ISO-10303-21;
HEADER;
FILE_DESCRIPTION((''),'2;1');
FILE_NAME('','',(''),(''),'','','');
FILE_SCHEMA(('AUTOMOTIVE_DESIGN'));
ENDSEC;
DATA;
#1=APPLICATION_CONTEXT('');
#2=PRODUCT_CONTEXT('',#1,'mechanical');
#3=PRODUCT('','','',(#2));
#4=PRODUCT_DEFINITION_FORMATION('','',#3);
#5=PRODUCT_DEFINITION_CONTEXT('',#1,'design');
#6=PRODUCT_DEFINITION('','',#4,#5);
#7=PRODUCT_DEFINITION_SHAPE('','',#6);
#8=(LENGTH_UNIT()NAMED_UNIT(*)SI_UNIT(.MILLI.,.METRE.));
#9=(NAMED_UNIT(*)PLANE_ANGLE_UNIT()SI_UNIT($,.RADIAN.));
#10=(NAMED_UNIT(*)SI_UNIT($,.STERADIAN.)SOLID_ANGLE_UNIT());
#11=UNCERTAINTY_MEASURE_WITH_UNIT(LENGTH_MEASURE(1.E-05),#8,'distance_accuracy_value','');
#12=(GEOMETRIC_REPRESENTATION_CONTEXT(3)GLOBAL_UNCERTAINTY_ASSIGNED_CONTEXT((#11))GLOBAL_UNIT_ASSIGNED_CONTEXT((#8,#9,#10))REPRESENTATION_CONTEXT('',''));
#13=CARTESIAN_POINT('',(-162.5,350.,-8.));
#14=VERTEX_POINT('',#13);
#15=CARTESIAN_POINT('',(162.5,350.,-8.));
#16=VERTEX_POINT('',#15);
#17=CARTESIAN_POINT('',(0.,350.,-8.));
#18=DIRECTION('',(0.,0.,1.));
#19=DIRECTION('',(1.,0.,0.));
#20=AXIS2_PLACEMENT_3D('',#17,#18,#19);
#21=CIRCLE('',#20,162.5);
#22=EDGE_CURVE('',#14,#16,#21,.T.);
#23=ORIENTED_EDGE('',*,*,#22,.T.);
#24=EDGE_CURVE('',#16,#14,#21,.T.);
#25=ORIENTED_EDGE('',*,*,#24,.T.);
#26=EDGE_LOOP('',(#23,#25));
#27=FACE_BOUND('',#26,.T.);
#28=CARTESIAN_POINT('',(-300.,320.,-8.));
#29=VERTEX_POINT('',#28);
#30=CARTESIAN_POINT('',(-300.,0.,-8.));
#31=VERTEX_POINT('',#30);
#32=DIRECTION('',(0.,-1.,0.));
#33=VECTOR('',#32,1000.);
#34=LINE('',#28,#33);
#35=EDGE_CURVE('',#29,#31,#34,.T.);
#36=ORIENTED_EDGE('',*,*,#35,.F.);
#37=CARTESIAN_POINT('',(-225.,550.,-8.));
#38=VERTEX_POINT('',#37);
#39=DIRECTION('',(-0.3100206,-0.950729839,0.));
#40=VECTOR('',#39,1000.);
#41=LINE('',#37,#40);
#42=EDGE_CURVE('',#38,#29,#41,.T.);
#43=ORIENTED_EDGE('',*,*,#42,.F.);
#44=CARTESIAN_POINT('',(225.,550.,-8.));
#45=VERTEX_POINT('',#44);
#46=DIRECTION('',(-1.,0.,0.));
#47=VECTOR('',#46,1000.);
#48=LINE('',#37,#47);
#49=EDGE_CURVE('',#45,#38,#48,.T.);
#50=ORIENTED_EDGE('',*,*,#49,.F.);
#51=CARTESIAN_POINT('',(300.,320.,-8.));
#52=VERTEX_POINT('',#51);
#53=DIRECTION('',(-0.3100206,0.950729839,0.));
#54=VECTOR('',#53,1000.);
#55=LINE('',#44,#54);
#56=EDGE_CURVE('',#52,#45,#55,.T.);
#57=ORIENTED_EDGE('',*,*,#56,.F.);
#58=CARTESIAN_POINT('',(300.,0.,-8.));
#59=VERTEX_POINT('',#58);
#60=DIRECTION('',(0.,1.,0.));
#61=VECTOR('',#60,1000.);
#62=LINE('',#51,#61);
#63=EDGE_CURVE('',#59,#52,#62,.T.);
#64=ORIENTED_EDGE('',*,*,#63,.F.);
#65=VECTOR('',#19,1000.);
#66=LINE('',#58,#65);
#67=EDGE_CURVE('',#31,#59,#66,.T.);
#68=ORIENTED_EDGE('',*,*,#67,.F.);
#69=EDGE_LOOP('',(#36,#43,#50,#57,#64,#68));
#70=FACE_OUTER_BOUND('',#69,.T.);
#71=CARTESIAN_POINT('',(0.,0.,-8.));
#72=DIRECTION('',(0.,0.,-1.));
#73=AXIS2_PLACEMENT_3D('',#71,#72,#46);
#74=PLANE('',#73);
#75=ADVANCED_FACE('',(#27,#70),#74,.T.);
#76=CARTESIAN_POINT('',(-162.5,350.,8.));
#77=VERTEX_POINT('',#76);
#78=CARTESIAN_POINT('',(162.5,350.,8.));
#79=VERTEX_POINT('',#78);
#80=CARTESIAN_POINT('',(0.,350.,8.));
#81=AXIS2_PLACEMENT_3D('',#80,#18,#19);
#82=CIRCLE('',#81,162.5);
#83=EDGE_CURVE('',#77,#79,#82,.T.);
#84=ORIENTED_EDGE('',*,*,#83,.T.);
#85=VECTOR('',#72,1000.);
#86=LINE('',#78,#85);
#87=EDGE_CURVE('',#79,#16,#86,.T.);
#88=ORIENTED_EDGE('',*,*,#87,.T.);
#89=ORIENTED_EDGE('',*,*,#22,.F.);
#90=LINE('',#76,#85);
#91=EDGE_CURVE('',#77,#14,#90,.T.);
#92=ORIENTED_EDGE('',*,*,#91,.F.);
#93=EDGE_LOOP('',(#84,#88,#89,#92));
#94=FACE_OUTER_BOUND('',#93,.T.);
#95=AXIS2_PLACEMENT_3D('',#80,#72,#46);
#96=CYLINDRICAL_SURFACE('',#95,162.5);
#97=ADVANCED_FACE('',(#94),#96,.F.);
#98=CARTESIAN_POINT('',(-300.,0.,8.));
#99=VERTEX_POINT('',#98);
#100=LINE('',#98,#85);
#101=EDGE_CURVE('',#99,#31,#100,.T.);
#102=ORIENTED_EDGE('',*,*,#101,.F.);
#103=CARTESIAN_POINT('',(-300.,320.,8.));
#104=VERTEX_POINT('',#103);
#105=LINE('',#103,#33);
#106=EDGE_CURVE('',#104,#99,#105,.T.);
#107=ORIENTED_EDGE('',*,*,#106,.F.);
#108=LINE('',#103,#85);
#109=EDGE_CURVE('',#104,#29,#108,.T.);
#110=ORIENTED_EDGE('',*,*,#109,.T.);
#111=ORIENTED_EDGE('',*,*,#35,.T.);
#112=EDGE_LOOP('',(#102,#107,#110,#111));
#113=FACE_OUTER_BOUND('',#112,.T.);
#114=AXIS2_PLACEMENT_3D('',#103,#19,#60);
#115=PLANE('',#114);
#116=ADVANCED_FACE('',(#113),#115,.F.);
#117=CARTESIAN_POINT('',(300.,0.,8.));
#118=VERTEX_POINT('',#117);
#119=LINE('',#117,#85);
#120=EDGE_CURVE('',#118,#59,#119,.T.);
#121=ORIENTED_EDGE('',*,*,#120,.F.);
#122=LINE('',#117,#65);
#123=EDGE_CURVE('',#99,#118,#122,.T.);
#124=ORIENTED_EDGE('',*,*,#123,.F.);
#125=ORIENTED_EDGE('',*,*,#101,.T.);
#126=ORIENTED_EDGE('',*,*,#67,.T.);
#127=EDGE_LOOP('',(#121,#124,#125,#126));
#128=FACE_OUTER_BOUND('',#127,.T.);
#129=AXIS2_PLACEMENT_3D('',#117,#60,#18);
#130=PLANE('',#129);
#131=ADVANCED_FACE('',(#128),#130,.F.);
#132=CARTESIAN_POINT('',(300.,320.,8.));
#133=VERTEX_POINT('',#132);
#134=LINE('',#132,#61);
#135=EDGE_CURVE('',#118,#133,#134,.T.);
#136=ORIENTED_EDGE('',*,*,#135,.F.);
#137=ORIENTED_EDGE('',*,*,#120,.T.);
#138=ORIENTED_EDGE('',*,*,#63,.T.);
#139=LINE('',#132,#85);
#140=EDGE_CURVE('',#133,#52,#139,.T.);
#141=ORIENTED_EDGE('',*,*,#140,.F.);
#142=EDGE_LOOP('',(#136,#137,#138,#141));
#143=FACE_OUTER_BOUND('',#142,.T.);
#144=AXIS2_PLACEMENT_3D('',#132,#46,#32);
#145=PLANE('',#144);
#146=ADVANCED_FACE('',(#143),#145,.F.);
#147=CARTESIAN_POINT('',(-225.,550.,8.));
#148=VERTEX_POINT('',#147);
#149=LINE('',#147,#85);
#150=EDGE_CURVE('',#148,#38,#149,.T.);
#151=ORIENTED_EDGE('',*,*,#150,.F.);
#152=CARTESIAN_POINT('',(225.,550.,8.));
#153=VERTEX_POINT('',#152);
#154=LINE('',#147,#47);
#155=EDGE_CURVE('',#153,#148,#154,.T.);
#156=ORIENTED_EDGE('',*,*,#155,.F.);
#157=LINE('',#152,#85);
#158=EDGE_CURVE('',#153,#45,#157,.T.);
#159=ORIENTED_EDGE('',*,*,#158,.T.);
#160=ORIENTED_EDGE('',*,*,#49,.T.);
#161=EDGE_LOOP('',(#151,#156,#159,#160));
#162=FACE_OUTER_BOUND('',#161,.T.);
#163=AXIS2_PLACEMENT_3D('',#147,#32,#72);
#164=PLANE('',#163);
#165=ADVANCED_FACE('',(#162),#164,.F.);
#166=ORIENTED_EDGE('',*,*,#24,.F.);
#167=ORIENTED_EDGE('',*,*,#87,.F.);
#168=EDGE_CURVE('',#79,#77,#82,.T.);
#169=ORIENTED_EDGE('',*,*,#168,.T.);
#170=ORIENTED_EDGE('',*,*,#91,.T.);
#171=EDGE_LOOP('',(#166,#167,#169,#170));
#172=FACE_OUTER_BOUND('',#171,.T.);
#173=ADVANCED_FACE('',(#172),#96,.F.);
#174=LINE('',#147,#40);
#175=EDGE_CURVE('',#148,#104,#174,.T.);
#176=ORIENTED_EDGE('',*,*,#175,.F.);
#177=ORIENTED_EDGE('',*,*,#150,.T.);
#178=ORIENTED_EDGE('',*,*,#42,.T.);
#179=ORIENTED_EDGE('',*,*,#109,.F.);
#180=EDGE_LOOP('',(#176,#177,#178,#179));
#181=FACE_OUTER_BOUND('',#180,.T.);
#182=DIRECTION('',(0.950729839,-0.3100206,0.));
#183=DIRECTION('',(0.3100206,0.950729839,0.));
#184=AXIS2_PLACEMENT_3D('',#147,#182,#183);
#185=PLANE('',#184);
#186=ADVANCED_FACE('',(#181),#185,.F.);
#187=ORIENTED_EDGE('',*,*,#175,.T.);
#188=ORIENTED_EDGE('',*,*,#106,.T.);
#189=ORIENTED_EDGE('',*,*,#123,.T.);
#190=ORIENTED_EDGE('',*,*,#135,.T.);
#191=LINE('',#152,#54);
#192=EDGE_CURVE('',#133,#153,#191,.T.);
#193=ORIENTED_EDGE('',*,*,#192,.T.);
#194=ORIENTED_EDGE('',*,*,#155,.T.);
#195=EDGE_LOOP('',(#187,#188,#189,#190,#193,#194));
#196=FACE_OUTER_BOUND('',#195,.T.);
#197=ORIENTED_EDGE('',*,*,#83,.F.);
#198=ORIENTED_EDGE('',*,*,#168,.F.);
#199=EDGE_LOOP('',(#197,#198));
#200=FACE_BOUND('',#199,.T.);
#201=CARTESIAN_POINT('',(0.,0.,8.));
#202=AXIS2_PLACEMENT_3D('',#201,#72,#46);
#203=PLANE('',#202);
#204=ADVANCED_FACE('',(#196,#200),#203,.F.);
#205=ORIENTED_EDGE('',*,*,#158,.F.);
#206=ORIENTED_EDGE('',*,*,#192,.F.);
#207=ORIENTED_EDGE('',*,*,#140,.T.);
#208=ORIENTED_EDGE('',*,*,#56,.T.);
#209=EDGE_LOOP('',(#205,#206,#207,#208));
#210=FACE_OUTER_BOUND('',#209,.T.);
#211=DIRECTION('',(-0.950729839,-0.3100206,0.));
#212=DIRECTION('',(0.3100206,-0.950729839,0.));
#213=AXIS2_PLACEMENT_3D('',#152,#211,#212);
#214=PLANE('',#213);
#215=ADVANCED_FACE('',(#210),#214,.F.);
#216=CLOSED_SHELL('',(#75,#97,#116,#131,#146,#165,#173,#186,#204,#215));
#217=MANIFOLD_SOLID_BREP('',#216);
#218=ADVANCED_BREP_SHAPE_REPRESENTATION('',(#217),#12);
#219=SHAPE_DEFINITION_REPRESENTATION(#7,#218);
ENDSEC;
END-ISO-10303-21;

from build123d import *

# Parameters (mm, degrees)
SKETCH1_R           = 162.5
BOSS_EXTRUDE1_DEPTH = 8


with BuildPart() as part:
    # Sketch1 → Boss-Extrude1 (new, symmetric)
    with BuildSketch(Plane.XY):
        Polygon((-225, 550), (225, 550), (300, 320), (300, 0), (-300, 0), (-300, 320), align=None)
        with Locations((0, 350)):
            Circle(SKETCH1_R, mode=Mode.SUBTRACT)
    extrude(amount=BOSS_EXTRUDE1_DEPTH, both=True)


solid = part.part
